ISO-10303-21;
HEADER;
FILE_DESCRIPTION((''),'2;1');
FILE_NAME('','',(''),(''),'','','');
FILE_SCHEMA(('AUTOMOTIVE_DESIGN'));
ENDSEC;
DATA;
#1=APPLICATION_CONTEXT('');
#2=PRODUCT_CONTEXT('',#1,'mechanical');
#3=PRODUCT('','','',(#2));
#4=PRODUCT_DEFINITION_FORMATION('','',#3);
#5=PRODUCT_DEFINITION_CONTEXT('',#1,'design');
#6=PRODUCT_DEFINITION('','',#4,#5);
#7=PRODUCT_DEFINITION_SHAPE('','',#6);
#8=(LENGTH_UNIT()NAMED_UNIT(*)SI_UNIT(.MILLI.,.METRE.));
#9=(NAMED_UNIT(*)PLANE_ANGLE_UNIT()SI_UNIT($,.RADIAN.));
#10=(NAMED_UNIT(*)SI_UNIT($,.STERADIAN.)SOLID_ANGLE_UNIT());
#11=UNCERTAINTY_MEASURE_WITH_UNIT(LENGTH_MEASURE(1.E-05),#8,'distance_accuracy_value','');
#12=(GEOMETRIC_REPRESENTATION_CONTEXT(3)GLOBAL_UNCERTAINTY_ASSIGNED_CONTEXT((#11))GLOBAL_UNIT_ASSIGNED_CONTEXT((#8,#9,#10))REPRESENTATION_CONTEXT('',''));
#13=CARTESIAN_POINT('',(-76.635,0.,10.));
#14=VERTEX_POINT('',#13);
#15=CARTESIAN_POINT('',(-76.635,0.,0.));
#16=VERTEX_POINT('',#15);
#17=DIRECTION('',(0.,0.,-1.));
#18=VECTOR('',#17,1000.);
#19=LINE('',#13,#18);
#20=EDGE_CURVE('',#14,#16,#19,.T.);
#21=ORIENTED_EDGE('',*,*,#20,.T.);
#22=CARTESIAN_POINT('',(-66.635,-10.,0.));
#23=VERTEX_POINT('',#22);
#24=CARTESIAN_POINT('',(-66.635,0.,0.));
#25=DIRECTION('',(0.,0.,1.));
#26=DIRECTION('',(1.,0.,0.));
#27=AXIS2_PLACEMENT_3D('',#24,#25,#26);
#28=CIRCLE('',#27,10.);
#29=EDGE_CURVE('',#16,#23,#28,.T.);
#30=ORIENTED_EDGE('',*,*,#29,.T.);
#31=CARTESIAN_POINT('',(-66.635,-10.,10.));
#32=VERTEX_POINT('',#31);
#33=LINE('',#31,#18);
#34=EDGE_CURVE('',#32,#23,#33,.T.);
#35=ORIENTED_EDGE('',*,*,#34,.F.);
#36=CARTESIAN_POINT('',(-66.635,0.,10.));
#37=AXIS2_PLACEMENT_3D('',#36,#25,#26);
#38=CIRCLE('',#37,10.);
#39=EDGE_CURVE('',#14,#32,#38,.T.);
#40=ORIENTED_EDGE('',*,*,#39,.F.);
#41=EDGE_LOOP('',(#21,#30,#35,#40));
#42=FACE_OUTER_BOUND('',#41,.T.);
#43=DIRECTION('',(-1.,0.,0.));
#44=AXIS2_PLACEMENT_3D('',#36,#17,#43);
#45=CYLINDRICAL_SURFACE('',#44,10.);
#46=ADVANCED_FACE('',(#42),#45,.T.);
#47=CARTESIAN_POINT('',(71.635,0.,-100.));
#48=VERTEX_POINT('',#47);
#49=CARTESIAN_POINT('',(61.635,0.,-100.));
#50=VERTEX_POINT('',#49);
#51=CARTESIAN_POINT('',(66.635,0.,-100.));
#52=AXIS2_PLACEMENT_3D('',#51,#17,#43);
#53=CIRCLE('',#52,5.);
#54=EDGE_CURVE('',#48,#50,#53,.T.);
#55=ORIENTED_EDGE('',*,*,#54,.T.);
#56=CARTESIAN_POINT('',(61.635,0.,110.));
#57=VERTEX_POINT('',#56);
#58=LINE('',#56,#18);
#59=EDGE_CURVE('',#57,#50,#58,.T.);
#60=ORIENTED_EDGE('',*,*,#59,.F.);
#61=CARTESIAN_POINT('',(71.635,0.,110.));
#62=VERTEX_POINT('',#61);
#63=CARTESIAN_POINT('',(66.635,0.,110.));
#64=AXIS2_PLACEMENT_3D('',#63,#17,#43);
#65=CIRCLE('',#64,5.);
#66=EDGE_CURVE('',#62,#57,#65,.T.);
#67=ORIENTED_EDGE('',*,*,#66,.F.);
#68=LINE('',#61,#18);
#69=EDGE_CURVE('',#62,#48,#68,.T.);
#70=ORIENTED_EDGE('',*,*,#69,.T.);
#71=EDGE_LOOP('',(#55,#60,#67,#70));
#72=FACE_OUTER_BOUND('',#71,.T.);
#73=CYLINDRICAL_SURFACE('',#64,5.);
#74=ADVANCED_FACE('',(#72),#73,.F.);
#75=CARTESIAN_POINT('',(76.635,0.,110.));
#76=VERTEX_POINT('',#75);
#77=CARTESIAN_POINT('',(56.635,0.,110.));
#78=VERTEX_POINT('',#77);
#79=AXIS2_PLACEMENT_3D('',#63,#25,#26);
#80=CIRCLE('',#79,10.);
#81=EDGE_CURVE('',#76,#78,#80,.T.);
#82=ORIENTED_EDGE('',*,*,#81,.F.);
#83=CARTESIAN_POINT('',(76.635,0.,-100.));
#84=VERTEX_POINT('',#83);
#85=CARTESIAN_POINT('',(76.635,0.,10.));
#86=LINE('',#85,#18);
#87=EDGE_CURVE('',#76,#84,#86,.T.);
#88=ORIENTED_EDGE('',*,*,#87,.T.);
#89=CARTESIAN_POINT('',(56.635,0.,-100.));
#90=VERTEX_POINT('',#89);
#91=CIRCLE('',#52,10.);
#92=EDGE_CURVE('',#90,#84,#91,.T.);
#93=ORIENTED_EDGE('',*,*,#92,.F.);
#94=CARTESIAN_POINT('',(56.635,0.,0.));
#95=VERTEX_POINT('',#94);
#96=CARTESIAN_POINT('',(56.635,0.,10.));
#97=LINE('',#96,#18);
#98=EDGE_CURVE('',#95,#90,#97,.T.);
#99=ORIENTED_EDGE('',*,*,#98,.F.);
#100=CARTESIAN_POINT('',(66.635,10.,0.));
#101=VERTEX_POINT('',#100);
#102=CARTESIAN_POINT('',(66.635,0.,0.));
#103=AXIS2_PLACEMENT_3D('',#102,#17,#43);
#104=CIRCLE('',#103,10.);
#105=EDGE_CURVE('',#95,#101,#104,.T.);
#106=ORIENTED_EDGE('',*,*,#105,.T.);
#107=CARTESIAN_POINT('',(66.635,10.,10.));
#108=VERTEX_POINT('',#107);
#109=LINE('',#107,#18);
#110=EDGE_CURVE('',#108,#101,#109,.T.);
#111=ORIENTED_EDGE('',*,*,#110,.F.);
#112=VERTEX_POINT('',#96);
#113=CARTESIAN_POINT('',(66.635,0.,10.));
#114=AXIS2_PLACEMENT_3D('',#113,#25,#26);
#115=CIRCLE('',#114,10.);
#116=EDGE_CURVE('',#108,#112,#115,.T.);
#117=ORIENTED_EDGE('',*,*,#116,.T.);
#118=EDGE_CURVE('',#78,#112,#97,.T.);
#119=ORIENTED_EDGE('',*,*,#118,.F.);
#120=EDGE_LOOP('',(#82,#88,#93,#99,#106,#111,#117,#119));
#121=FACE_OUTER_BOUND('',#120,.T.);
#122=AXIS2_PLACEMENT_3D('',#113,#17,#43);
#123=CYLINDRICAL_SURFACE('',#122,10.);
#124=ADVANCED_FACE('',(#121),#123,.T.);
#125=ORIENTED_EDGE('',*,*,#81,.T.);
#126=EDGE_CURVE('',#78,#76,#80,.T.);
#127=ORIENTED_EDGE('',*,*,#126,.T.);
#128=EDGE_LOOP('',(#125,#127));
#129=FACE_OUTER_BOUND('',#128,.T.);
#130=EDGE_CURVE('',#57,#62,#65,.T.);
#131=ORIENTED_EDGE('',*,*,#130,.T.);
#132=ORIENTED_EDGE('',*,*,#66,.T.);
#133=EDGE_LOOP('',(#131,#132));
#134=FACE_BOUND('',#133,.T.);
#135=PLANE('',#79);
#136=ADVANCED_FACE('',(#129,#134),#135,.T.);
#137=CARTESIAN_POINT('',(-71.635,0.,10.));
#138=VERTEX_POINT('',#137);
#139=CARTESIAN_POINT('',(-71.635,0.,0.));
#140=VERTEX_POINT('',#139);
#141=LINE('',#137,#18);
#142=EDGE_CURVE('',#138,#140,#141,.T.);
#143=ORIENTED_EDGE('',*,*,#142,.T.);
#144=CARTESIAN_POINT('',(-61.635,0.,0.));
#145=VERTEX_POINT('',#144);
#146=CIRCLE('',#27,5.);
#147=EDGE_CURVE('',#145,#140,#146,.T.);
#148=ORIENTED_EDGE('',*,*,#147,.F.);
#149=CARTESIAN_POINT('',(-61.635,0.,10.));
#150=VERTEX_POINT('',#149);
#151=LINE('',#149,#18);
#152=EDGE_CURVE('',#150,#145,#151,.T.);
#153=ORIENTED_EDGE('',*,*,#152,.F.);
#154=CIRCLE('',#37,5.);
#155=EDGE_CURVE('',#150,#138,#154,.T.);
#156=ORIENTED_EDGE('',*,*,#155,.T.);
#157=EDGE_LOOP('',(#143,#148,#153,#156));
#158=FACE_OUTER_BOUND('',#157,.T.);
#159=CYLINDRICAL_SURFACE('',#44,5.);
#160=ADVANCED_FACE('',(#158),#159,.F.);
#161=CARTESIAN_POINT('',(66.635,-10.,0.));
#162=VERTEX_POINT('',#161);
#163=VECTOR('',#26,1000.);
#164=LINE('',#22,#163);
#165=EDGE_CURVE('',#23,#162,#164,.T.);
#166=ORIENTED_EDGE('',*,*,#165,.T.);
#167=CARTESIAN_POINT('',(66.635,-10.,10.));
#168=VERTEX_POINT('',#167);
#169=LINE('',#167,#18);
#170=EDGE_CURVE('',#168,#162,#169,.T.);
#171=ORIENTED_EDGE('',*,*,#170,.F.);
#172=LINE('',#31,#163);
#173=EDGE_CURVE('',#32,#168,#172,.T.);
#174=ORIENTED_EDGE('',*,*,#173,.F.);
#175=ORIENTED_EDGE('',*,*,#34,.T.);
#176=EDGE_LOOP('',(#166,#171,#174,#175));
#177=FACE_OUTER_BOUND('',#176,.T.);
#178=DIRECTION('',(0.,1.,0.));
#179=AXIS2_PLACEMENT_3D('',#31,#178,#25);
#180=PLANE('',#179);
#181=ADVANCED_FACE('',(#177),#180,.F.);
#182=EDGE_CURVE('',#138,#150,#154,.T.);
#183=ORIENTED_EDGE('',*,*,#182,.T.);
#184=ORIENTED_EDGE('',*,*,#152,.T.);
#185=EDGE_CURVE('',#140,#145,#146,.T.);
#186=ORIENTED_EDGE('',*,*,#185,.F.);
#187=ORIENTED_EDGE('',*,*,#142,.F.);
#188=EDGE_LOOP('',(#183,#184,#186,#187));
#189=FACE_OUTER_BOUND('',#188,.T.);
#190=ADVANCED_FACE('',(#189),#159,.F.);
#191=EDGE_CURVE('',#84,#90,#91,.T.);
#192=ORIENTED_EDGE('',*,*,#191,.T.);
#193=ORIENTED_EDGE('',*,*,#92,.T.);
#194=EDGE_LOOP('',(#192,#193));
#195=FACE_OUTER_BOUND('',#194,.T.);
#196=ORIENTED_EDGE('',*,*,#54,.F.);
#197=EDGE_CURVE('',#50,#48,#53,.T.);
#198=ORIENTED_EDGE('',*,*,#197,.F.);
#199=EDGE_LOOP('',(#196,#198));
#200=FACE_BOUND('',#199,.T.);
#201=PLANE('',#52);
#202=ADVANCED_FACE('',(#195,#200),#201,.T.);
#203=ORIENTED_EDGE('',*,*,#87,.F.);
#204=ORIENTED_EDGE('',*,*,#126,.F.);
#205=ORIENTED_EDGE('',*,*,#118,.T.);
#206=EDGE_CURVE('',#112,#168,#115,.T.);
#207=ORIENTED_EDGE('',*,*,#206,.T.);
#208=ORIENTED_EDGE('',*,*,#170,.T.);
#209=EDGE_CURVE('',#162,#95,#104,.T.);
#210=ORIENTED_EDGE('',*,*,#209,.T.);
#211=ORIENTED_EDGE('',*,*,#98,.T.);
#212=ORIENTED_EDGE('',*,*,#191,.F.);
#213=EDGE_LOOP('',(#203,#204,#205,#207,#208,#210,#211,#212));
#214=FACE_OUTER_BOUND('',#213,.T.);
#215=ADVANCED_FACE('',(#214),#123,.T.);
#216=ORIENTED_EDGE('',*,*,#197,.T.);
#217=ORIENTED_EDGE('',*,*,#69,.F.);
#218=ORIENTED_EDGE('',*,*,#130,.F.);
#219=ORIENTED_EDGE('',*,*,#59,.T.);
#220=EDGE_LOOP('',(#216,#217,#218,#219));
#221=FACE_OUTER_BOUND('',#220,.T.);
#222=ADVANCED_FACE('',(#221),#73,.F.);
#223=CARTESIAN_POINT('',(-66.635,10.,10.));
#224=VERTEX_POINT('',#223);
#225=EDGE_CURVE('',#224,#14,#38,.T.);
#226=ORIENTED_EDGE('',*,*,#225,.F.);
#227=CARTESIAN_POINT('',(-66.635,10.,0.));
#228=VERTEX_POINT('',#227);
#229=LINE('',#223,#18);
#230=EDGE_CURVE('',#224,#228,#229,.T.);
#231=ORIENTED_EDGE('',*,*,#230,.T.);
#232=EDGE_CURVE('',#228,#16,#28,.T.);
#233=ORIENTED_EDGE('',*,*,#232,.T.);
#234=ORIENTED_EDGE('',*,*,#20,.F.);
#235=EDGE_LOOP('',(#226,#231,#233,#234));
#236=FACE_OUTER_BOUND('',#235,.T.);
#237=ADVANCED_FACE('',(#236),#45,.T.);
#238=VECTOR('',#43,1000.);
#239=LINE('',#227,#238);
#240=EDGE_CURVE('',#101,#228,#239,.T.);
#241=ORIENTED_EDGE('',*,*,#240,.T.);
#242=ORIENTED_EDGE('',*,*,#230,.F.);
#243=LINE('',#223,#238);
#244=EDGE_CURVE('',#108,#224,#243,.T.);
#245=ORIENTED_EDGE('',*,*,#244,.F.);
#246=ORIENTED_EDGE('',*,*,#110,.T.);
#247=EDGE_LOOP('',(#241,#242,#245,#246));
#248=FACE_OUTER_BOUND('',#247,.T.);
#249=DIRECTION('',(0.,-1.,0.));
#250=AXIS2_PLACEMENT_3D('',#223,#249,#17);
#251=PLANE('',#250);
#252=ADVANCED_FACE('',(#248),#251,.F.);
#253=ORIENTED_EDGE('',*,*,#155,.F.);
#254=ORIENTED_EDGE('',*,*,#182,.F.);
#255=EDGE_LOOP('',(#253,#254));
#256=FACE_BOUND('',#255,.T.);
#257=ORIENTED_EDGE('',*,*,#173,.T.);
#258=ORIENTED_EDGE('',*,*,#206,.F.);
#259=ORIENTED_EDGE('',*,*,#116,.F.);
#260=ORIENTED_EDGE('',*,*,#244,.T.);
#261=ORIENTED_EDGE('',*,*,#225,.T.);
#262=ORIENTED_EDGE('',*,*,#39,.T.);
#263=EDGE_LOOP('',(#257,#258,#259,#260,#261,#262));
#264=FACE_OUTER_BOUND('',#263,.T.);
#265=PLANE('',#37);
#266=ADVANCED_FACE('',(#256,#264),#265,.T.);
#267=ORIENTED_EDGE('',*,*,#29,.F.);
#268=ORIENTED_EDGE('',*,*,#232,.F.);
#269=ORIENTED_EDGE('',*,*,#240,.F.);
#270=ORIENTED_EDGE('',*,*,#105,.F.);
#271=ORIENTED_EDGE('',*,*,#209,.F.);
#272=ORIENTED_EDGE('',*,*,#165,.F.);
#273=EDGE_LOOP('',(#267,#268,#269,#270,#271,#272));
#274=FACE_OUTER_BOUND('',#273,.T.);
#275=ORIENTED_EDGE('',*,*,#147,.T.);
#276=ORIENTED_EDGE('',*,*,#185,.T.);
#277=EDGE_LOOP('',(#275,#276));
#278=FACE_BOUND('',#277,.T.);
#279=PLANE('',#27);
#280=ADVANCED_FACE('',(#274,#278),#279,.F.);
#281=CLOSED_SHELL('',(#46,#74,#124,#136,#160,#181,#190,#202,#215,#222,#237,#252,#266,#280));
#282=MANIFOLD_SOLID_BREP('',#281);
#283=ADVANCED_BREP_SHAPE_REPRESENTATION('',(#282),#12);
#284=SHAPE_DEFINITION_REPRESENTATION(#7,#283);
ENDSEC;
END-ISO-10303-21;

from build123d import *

# Parameters (mm, degrees)
SKETCH_1_R               = 5
SKETCH_1_R_2             = 4.376095709
EXTRUDE_1_DEPTH          = 10
SKETCH_2_R               = 10
EXTRUDE_2_DEPTH          = 100
EXTRUDE_START            = 100
SKETCH_3_R               = 10
EXTRUDE_3_DEPTH          = 100
CUT_EXTRUDE_1_DEPTH      = 224.769799627
CUT_EXTRUDE_1_DEPTH_BACK = 224.769799627
SKETCH_4_R               = 5


with BuildPart() as part:
    # 草图1 → 凸台-拉伸1 (new body)
    with BuildSketch(Plane.XY):
        with BuildLine():
            Line((-66.635, 10), (66.635, 10))
            ThreePointArc((66.635, 10), (76.635, 0), (66.635, -10))
            Line((66.635, -10), (-66.635, -10))
            ThreePointArc((-66.635, -10), (-76.635, 0), (-66.635, 10))
        make_face()
        with Locations((-66.635, 0)):
            Circle(SKETCH_1_R, mode=Mode.SUBTRACT)
        with Locations((66.635, 0)):
            Circle(SKETCH_1_R_2, mode=Mode.SUBTRACT)
    extrude(amount=EXTRUDE_1_DEPTH)

    # 草图2 → 凸台-拉伸2 (add)
    with BuildSketch(Plane.XY.offset(10)):
        with Locations(Location((66.635, 0, 0), (0, 0, 90))):
            Circle(SKETCH_2_R)
    extrude(amount=EXTRUDE_2_DEPTH)

    # 草图3 → 凸台-拉伸3 (add)
    with BuildSketch(Plane(origin=(0, 0, 0), x_dir=(-1, 0, 0), z_dir=(0, 0, -1)).offset(EXTRUDE_START)):
        with Locations((-66.635, 0)):
            Circle(SKETCH_3_R)
    extrude(amount=-EXTRUDE_3_DEPTH)

    # 草图4 → 切除-拉伸1 (cut, two sides: drawn at the far end of the back side and taken through both)
    with BuildSketch(Plane(origin=(0, 0, -100), x_dir=(-1, 0, 0), z_dir=(0, 0, -1)).offset(-CUT_EXTRUDE_1_DEPTH_BACK)):
        with Locations((-66.635, 0)):
            Circle(SKETCH_4_R)
    extrude(amount=CUT_EXTRUDE_1_DEPTH + CUT_EXTRUDE_1_DEPTH_BACK, mode=Mode.SUBTRACT)


solid = part.part
